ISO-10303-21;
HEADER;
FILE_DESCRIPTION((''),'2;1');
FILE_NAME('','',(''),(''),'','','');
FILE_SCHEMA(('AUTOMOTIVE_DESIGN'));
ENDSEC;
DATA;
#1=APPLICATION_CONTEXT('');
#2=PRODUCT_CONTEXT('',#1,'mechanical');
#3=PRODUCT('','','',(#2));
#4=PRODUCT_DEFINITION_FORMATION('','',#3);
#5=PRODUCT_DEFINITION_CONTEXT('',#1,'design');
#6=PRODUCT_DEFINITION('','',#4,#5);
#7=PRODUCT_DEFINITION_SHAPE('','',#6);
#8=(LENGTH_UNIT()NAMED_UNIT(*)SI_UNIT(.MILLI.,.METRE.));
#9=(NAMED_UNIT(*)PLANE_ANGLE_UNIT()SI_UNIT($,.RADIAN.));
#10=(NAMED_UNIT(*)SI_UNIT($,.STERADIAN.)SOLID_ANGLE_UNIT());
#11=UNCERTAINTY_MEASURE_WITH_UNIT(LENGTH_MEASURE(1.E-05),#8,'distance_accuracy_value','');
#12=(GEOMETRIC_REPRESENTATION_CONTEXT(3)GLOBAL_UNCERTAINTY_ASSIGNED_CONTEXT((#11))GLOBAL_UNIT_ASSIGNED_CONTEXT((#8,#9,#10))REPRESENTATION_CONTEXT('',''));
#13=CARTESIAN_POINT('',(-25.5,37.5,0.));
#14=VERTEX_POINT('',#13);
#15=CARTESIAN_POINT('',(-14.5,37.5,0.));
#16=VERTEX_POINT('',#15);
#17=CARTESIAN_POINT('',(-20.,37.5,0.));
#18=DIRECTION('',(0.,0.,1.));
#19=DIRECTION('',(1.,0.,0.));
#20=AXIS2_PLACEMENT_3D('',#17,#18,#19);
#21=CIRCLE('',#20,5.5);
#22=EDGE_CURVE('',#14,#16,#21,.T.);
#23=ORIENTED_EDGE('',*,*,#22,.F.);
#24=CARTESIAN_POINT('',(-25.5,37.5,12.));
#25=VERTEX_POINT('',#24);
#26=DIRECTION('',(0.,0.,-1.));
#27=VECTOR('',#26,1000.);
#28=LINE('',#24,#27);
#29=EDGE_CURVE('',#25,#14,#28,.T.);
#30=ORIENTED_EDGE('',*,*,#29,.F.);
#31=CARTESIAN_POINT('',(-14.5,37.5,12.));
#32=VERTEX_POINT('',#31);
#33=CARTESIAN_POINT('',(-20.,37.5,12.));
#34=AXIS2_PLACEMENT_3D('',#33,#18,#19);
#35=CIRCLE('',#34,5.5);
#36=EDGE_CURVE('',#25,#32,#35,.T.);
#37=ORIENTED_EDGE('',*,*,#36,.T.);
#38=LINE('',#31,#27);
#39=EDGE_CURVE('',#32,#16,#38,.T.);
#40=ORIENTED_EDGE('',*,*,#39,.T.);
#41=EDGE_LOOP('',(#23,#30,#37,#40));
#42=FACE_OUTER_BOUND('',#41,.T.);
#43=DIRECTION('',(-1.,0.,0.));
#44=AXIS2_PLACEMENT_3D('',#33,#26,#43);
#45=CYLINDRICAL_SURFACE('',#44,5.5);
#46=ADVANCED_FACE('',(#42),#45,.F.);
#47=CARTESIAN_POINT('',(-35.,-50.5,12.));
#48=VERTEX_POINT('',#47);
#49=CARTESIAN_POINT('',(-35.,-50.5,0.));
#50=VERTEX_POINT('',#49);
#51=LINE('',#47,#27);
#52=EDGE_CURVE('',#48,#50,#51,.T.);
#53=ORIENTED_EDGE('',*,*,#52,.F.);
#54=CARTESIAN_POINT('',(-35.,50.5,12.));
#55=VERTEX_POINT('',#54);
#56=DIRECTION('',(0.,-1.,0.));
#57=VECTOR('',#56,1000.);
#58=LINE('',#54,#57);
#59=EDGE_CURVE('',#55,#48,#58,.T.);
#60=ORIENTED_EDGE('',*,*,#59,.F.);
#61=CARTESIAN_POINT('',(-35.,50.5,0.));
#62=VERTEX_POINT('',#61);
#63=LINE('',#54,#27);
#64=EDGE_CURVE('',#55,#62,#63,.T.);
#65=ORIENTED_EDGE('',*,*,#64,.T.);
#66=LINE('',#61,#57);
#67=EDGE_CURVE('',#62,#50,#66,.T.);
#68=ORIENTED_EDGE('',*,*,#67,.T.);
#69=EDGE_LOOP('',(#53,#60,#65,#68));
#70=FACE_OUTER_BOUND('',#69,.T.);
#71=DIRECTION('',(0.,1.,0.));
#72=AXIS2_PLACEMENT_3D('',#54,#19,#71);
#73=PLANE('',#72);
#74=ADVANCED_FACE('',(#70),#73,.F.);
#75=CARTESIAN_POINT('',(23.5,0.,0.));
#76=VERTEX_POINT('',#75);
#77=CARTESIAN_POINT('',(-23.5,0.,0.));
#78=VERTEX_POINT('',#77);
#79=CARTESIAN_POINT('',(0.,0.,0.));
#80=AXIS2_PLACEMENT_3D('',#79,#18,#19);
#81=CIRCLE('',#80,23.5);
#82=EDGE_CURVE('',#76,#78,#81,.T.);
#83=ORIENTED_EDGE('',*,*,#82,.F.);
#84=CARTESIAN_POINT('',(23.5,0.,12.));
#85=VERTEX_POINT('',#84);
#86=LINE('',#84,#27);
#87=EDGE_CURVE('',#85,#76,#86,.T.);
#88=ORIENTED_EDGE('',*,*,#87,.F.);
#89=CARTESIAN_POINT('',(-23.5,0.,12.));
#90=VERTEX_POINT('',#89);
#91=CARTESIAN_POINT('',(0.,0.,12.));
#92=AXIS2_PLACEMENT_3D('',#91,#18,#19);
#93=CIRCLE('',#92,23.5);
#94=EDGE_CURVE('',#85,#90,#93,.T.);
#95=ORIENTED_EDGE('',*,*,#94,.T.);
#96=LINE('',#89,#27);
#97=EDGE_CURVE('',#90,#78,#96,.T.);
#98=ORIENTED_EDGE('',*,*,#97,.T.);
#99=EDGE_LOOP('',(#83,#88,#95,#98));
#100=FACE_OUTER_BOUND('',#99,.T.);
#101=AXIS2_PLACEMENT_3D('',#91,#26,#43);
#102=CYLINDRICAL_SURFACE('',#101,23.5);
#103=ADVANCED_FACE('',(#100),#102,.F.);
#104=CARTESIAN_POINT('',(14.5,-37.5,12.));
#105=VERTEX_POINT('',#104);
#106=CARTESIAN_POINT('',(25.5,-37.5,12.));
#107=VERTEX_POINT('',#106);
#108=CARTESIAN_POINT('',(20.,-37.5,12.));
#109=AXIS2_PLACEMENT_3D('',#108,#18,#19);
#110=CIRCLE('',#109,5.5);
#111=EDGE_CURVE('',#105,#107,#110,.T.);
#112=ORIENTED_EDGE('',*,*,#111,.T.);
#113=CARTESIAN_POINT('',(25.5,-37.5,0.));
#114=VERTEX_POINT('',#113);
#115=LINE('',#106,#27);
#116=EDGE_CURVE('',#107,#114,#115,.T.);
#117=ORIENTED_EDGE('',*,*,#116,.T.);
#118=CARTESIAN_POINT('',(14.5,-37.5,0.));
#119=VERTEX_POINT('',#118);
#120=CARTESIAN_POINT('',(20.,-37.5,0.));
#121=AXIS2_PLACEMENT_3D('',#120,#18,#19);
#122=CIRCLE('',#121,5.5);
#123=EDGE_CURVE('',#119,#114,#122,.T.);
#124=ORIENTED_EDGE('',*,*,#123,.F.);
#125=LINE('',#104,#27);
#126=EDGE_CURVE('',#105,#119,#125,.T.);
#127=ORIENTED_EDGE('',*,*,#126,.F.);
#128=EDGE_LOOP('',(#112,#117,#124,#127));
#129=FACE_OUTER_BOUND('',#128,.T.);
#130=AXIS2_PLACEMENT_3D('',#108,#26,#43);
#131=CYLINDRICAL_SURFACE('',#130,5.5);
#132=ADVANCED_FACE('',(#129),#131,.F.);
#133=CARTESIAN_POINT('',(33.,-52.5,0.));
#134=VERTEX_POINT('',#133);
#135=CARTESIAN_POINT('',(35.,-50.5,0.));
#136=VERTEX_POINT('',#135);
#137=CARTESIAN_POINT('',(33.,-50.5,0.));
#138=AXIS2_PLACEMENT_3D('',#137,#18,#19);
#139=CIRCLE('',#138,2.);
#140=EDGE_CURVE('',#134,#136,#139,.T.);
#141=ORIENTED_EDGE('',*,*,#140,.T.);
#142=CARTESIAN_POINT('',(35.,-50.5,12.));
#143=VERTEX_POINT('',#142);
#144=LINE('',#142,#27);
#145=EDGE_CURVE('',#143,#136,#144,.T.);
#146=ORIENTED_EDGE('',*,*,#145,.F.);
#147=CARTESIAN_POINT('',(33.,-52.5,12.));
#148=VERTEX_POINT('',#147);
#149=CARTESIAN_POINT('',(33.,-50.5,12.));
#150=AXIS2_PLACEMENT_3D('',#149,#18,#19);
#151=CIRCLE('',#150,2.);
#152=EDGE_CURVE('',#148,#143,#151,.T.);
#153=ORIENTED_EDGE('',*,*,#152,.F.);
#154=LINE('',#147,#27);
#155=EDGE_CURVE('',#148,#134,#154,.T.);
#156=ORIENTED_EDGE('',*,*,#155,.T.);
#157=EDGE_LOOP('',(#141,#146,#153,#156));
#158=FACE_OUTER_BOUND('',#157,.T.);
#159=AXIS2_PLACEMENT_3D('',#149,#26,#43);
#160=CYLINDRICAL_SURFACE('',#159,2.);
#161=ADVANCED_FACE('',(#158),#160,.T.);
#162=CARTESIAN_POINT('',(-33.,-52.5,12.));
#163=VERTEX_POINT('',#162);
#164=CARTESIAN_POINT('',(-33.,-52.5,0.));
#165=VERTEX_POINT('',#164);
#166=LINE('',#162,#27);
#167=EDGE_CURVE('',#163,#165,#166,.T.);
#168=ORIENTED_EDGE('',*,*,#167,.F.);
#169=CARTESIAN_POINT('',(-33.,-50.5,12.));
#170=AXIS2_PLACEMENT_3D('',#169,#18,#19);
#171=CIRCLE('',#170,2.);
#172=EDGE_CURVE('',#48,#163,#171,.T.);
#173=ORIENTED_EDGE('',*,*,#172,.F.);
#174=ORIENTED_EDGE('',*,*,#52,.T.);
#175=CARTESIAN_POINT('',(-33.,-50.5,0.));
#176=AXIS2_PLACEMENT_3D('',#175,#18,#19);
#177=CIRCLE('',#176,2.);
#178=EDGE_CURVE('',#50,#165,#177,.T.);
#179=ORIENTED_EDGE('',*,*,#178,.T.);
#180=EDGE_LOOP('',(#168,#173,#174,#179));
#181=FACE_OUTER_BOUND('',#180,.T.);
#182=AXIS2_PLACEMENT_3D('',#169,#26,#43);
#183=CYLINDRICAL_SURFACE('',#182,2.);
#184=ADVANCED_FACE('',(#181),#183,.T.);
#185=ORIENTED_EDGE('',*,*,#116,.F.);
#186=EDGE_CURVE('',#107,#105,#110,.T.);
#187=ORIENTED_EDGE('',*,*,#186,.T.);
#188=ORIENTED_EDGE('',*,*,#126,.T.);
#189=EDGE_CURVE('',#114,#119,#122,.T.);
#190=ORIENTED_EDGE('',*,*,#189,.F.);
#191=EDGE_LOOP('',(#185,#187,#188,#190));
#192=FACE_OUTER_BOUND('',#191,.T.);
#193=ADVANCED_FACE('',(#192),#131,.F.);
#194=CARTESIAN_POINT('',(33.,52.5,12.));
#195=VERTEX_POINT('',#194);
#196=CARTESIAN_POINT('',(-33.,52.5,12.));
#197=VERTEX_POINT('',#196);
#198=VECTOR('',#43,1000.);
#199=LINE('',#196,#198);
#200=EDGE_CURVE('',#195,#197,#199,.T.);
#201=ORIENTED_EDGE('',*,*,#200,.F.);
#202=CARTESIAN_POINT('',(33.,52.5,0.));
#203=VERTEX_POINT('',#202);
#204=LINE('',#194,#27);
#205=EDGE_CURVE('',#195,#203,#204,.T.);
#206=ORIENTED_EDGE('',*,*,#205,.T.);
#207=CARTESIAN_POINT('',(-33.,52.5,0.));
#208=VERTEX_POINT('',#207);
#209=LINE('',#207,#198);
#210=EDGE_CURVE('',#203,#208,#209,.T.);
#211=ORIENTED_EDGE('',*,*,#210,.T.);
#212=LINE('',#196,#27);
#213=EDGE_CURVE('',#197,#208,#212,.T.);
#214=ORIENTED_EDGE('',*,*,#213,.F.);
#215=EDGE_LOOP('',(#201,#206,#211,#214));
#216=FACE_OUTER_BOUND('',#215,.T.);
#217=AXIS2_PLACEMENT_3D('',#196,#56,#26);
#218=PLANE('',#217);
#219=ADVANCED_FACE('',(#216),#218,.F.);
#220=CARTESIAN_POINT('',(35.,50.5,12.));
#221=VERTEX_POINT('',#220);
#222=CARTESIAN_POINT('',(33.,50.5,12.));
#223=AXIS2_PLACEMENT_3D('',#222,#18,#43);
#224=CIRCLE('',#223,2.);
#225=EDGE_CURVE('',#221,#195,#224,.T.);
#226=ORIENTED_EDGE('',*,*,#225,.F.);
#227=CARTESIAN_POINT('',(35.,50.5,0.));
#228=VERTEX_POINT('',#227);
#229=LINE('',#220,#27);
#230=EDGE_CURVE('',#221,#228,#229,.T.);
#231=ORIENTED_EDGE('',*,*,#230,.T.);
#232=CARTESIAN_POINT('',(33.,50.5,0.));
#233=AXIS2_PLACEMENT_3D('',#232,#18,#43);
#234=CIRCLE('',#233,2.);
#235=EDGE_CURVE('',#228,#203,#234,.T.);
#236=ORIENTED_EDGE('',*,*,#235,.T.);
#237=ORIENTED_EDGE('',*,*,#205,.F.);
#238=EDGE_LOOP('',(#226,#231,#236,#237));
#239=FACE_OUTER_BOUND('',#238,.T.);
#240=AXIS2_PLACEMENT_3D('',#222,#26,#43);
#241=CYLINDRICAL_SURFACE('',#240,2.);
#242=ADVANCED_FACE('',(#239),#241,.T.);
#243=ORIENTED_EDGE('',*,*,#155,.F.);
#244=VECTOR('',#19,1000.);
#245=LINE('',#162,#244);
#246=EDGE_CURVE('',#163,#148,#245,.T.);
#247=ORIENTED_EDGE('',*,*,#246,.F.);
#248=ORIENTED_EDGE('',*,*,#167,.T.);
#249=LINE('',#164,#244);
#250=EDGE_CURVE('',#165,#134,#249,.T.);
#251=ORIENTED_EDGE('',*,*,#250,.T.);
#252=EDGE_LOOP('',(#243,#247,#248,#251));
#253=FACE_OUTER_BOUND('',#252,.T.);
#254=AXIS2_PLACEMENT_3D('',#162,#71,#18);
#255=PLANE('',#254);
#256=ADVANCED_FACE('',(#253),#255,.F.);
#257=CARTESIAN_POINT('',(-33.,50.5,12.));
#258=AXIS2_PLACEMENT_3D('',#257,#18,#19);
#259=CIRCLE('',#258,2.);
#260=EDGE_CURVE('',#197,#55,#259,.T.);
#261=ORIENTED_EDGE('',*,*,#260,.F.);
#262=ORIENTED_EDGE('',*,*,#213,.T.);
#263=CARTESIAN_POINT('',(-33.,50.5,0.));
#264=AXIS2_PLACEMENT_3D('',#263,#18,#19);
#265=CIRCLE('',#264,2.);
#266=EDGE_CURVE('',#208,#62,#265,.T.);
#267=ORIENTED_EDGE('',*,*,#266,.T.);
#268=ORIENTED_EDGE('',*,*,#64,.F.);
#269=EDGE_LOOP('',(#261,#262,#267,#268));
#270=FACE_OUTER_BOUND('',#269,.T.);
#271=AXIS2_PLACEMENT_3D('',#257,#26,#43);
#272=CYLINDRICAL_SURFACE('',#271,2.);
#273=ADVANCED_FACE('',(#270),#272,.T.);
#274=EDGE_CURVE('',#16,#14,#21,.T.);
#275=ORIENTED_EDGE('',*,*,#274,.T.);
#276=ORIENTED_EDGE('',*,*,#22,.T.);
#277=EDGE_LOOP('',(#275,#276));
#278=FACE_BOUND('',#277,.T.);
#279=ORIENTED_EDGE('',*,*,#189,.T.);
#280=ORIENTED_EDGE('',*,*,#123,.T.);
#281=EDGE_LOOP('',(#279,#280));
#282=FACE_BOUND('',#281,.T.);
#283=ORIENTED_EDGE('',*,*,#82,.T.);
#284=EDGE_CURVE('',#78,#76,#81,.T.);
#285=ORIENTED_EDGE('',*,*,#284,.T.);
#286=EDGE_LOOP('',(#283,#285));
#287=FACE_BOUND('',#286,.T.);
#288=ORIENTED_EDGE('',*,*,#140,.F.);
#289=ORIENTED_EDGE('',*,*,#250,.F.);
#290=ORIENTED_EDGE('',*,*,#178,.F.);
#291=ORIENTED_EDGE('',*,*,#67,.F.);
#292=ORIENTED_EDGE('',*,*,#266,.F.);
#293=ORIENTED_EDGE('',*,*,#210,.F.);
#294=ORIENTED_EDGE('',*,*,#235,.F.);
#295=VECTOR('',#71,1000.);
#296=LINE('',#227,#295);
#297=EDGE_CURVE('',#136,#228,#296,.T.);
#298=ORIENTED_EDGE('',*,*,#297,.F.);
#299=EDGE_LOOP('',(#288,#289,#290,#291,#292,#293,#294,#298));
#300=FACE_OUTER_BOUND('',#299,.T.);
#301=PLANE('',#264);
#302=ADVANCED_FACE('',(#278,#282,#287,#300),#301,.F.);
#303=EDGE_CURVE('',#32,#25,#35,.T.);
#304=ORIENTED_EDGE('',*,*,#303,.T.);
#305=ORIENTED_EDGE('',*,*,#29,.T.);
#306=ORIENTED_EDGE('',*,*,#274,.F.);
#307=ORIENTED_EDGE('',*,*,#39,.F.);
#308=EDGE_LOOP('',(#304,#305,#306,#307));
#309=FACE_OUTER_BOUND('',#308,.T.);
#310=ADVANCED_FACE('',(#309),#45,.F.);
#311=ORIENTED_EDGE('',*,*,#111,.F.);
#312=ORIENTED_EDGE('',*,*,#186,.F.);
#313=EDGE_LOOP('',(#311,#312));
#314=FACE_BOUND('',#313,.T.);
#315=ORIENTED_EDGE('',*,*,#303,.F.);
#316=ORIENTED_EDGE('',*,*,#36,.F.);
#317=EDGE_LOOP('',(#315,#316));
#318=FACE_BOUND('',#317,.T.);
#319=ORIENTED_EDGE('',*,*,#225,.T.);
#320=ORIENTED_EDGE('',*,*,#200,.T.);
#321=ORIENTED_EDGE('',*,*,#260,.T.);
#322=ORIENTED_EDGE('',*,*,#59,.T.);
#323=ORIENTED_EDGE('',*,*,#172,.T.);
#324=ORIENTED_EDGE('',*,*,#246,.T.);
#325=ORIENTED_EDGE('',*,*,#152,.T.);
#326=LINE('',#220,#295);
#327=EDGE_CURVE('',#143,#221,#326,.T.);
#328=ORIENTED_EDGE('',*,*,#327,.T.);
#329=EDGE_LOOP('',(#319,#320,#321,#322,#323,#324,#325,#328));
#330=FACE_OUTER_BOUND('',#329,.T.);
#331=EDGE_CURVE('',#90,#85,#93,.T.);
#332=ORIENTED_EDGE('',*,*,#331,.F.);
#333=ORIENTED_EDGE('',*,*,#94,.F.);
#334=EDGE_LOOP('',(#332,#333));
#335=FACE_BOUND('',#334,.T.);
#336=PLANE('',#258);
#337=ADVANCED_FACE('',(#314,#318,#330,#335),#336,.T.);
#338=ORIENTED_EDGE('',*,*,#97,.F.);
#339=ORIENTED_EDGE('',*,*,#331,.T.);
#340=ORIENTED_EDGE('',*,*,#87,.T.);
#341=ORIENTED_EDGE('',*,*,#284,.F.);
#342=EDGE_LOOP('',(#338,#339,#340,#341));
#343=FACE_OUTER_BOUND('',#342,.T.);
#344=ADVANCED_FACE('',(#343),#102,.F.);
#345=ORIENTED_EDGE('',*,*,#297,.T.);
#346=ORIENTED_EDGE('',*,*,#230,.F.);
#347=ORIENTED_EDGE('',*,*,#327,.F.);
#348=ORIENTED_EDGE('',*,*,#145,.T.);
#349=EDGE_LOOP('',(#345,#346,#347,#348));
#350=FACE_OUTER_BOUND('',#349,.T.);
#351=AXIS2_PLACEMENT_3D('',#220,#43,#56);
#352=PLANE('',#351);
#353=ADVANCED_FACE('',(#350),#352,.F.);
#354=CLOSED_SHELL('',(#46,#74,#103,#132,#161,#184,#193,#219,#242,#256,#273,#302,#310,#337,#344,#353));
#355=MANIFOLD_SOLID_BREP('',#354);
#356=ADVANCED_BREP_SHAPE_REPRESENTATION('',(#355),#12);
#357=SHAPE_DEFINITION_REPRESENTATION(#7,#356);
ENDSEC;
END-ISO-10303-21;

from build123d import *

# Parameters (mm, degrees)
SKETCH_1_R      = 23.5
SKETCH_1_R_2    = 5.5
EXTRUDE_1_DEPTH = 12


with BuildPart() as part:
    # 草图1 → 凸台-拉伸1 (new body)
    with BuildSketch(Plane.XY):
        with BuildLine():
            Line((-33, 52.5), (33, 52.5))
            ThreePointArc((33, 52.5), (34.414213562, 51.914213562), (35, 50.5))
            Line((35, 50.5), (35, -50.5))
            ThreePointArc((35, -50.5), (34.414213562, -51.914213562), (33, -52.5))
            Line((33, -52.5), (-33, -52.5))
            ThreePointArc((-33, -52.5), (-34.414213562, -51.914213562), (-35, -50.5))
            Line((-35, -50.5), (-35, 50.5))
            ThreePointArc((-35, 50.5), (-34.414213562, 51.914213562), (-33, 52.5))
        make_face()
        Circle(SKETCH_1_R, mode=Mode.SUBTRACT)
        with Locations((-20, 37.5)):
            Circle(SKETCH_1_R_2, mode=Mode.SUBTRACT)
        with Locations((20, -37.5)):
            Circle(SKETCH_1_R_2, mode=Mode.SUBTRACT)
    extrude(amount=EXTRUDE_1_DEPTH)


solid = part.part
